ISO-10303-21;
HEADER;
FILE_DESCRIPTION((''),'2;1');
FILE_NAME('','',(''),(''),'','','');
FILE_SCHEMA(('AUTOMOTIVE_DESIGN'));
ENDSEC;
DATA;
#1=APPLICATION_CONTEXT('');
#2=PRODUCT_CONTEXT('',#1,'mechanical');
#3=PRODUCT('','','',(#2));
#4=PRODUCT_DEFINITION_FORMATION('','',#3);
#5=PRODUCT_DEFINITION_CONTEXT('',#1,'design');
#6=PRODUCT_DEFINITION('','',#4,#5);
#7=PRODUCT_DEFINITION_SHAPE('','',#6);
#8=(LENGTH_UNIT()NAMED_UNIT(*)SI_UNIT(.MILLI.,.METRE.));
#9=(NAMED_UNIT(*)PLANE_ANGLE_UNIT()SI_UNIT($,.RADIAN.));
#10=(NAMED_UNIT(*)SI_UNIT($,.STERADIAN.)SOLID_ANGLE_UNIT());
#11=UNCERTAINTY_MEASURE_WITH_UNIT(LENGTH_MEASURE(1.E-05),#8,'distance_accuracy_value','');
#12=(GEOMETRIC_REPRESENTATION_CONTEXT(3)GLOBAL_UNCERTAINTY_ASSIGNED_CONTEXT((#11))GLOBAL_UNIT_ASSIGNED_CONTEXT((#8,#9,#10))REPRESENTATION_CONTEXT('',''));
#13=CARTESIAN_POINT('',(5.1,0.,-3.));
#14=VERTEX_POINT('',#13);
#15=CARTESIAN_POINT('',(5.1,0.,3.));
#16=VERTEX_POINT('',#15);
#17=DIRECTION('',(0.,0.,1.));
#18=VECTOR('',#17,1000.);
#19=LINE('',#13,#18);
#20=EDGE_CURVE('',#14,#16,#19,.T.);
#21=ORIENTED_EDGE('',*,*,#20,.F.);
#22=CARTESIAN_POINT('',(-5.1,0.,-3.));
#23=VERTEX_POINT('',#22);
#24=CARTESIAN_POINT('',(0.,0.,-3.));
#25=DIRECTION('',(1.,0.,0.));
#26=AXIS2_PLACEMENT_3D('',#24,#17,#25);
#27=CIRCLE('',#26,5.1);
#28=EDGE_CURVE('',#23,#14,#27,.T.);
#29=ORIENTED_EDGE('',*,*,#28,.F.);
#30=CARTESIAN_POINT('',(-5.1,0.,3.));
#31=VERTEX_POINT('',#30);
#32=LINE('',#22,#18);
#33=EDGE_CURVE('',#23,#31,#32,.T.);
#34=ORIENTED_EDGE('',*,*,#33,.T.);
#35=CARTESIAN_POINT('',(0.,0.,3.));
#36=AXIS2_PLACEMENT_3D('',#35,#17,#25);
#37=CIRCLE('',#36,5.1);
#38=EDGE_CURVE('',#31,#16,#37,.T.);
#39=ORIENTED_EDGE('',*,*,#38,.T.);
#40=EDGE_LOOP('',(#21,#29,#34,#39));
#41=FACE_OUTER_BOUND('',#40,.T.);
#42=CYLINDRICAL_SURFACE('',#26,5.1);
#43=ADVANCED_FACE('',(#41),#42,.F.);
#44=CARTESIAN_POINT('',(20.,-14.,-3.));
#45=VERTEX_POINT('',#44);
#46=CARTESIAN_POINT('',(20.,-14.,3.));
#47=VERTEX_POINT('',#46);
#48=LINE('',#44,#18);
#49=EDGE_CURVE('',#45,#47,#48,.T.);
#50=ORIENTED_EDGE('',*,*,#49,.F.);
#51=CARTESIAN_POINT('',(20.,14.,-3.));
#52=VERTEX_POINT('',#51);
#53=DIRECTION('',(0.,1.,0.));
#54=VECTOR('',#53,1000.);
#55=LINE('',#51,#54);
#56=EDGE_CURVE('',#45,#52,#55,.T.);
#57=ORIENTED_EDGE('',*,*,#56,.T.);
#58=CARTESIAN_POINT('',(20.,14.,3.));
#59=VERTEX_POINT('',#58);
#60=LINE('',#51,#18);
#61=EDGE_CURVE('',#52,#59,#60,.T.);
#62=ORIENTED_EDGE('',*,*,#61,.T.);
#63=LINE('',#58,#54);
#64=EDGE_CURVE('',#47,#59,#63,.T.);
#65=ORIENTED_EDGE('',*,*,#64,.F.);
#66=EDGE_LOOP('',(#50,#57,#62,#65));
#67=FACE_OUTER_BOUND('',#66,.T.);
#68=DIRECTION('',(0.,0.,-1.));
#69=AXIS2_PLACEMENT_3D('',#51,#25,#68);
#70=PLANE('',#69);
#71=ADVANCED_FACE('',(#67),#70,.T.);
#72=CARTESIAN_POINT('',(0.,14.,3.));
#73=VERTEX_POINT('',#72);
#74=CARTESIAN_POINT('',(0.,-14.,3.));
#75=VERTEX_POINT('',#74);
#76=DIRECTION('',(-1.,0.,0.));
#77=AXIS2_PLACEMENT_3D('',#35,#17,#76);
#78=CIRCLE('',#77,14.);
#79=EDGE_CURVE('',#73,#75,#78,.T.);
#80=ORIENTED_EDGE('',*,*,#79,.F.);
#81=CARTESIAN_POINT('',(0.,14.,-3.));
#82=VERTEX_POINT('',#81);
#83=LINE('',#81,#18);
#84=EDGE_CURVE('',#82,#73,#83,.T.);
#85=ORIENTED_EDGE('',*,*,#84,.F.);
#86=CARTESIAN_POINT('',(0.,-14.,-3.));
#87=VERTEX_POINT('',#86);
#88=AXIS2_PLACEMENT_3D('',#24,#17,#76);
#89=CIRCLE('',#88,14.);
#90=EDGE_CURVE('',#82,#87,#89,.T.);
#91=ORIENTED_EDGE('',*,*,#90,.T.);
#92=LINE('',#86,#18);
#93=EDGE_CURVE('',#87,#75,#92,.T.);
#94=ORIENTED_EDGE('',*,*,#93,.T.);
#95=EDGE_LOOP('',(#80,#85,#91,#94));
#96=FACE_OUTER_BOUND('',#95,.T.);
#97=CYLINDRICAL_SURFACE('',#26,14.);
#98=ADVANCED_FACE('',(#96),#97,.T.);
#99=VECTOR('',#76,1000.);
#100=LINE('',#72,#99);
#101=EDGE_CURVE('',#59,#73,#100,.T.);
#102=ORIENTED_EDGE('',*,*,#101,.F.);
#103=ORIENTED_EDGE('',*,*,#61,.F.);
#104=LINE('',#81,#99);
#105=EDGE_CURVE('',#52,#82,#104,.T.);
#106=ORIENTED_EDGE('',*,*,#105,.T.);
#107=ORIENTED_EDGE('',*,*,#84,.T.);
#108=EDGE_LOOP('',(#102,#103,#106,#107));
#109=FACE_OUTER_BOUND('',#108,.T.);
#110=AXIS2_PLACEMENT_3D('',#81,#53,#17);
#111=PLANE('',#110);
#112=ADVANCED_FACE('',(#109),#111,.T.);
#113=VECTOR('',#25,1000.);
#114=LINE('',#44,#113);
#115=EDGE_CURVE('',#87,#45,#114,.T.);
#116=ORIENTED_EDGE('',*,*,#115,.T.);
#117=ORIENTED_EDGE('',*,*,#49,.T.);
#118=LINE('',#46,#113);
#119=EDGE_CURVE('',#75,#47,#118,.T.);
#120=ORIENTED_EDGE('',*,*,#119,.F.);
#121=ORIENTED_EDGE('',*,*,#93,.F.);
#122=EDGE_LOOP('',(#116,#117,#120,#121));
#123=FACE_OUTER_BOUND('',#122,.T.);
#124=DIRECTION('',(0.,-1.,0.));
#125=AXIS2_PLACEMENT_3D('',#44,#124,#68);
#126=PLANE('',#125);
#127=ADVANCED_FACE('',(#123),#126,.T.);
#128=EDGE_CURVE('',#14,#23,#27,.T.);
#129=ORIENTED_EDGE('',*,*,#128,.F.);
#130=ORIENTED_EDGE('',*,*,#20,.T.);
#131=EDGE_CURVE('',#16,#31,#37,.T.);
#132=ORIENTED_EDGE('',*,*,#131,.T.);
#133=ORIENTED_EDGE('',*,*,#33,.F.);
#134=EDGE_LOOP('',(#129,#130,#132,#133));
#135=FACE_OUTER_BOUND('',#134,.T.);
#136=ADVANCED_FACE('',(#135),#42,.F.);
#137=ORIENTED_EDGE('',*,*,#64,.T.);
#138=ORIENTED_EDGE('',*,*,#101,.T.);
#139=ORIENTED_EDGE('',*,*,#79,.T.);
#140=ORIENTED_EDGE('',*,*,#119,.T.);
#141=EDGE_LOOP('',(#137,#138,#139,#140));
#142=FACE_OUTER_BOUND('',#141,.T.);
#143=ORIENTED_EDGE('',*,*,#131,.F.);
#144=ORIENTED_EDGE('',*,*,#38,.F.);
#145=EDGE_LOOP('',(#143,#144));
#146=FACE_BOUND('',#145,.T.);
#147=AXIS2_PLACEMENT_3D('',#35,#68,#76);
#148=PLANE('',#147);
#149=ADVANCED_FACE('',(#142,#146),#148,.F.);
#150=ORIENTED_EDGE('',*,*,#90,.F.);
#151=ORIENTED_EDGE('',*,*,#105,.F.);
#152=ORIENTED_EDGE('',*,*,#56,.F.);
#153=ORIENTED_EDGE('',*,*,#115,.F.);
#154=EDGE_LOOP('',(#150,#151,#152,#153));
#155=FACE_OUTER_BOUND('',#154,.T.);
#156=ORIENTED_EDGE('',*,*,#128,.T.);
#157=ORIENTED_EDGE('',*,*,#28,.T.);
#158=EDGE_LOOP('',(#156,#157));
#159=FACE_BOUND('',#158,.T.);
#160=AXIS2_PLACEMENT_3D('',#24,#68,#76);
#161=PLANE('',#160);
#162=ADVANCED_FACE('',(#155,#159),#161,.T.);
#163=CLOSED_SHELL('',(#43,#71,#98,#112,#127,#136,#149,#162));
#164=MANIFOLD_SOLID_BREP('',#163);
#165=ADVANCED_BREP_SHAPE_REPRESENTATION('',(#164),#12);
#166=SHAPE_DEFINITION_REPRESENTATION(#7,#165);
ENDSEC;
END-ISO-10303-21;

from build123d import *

# Parameters (mm, degrees)
SKETCH_1_R      = 5.1
EXTRUDE_1_DEPTH = 3


with BuildPart() as part:
    # 草图1 → 凸台-拉伸1 (new, symmetric)
    with BuildSketch(Plane.XY):
        with BuildLine():
            Line((0, 14), (20, 14))
            Line((20, 14), (20, -14))
            Line((20, -14), (0, -14))
            ThreePointArc((0, -14), (-14, 0), (0, 14))
        make_face()
        Circle(SKETCH_1_R, mode=Mode.SUBTRACT)
    extrude(amount=EXTRUDE_1_DEPTH, both=True)


solid = part.part
